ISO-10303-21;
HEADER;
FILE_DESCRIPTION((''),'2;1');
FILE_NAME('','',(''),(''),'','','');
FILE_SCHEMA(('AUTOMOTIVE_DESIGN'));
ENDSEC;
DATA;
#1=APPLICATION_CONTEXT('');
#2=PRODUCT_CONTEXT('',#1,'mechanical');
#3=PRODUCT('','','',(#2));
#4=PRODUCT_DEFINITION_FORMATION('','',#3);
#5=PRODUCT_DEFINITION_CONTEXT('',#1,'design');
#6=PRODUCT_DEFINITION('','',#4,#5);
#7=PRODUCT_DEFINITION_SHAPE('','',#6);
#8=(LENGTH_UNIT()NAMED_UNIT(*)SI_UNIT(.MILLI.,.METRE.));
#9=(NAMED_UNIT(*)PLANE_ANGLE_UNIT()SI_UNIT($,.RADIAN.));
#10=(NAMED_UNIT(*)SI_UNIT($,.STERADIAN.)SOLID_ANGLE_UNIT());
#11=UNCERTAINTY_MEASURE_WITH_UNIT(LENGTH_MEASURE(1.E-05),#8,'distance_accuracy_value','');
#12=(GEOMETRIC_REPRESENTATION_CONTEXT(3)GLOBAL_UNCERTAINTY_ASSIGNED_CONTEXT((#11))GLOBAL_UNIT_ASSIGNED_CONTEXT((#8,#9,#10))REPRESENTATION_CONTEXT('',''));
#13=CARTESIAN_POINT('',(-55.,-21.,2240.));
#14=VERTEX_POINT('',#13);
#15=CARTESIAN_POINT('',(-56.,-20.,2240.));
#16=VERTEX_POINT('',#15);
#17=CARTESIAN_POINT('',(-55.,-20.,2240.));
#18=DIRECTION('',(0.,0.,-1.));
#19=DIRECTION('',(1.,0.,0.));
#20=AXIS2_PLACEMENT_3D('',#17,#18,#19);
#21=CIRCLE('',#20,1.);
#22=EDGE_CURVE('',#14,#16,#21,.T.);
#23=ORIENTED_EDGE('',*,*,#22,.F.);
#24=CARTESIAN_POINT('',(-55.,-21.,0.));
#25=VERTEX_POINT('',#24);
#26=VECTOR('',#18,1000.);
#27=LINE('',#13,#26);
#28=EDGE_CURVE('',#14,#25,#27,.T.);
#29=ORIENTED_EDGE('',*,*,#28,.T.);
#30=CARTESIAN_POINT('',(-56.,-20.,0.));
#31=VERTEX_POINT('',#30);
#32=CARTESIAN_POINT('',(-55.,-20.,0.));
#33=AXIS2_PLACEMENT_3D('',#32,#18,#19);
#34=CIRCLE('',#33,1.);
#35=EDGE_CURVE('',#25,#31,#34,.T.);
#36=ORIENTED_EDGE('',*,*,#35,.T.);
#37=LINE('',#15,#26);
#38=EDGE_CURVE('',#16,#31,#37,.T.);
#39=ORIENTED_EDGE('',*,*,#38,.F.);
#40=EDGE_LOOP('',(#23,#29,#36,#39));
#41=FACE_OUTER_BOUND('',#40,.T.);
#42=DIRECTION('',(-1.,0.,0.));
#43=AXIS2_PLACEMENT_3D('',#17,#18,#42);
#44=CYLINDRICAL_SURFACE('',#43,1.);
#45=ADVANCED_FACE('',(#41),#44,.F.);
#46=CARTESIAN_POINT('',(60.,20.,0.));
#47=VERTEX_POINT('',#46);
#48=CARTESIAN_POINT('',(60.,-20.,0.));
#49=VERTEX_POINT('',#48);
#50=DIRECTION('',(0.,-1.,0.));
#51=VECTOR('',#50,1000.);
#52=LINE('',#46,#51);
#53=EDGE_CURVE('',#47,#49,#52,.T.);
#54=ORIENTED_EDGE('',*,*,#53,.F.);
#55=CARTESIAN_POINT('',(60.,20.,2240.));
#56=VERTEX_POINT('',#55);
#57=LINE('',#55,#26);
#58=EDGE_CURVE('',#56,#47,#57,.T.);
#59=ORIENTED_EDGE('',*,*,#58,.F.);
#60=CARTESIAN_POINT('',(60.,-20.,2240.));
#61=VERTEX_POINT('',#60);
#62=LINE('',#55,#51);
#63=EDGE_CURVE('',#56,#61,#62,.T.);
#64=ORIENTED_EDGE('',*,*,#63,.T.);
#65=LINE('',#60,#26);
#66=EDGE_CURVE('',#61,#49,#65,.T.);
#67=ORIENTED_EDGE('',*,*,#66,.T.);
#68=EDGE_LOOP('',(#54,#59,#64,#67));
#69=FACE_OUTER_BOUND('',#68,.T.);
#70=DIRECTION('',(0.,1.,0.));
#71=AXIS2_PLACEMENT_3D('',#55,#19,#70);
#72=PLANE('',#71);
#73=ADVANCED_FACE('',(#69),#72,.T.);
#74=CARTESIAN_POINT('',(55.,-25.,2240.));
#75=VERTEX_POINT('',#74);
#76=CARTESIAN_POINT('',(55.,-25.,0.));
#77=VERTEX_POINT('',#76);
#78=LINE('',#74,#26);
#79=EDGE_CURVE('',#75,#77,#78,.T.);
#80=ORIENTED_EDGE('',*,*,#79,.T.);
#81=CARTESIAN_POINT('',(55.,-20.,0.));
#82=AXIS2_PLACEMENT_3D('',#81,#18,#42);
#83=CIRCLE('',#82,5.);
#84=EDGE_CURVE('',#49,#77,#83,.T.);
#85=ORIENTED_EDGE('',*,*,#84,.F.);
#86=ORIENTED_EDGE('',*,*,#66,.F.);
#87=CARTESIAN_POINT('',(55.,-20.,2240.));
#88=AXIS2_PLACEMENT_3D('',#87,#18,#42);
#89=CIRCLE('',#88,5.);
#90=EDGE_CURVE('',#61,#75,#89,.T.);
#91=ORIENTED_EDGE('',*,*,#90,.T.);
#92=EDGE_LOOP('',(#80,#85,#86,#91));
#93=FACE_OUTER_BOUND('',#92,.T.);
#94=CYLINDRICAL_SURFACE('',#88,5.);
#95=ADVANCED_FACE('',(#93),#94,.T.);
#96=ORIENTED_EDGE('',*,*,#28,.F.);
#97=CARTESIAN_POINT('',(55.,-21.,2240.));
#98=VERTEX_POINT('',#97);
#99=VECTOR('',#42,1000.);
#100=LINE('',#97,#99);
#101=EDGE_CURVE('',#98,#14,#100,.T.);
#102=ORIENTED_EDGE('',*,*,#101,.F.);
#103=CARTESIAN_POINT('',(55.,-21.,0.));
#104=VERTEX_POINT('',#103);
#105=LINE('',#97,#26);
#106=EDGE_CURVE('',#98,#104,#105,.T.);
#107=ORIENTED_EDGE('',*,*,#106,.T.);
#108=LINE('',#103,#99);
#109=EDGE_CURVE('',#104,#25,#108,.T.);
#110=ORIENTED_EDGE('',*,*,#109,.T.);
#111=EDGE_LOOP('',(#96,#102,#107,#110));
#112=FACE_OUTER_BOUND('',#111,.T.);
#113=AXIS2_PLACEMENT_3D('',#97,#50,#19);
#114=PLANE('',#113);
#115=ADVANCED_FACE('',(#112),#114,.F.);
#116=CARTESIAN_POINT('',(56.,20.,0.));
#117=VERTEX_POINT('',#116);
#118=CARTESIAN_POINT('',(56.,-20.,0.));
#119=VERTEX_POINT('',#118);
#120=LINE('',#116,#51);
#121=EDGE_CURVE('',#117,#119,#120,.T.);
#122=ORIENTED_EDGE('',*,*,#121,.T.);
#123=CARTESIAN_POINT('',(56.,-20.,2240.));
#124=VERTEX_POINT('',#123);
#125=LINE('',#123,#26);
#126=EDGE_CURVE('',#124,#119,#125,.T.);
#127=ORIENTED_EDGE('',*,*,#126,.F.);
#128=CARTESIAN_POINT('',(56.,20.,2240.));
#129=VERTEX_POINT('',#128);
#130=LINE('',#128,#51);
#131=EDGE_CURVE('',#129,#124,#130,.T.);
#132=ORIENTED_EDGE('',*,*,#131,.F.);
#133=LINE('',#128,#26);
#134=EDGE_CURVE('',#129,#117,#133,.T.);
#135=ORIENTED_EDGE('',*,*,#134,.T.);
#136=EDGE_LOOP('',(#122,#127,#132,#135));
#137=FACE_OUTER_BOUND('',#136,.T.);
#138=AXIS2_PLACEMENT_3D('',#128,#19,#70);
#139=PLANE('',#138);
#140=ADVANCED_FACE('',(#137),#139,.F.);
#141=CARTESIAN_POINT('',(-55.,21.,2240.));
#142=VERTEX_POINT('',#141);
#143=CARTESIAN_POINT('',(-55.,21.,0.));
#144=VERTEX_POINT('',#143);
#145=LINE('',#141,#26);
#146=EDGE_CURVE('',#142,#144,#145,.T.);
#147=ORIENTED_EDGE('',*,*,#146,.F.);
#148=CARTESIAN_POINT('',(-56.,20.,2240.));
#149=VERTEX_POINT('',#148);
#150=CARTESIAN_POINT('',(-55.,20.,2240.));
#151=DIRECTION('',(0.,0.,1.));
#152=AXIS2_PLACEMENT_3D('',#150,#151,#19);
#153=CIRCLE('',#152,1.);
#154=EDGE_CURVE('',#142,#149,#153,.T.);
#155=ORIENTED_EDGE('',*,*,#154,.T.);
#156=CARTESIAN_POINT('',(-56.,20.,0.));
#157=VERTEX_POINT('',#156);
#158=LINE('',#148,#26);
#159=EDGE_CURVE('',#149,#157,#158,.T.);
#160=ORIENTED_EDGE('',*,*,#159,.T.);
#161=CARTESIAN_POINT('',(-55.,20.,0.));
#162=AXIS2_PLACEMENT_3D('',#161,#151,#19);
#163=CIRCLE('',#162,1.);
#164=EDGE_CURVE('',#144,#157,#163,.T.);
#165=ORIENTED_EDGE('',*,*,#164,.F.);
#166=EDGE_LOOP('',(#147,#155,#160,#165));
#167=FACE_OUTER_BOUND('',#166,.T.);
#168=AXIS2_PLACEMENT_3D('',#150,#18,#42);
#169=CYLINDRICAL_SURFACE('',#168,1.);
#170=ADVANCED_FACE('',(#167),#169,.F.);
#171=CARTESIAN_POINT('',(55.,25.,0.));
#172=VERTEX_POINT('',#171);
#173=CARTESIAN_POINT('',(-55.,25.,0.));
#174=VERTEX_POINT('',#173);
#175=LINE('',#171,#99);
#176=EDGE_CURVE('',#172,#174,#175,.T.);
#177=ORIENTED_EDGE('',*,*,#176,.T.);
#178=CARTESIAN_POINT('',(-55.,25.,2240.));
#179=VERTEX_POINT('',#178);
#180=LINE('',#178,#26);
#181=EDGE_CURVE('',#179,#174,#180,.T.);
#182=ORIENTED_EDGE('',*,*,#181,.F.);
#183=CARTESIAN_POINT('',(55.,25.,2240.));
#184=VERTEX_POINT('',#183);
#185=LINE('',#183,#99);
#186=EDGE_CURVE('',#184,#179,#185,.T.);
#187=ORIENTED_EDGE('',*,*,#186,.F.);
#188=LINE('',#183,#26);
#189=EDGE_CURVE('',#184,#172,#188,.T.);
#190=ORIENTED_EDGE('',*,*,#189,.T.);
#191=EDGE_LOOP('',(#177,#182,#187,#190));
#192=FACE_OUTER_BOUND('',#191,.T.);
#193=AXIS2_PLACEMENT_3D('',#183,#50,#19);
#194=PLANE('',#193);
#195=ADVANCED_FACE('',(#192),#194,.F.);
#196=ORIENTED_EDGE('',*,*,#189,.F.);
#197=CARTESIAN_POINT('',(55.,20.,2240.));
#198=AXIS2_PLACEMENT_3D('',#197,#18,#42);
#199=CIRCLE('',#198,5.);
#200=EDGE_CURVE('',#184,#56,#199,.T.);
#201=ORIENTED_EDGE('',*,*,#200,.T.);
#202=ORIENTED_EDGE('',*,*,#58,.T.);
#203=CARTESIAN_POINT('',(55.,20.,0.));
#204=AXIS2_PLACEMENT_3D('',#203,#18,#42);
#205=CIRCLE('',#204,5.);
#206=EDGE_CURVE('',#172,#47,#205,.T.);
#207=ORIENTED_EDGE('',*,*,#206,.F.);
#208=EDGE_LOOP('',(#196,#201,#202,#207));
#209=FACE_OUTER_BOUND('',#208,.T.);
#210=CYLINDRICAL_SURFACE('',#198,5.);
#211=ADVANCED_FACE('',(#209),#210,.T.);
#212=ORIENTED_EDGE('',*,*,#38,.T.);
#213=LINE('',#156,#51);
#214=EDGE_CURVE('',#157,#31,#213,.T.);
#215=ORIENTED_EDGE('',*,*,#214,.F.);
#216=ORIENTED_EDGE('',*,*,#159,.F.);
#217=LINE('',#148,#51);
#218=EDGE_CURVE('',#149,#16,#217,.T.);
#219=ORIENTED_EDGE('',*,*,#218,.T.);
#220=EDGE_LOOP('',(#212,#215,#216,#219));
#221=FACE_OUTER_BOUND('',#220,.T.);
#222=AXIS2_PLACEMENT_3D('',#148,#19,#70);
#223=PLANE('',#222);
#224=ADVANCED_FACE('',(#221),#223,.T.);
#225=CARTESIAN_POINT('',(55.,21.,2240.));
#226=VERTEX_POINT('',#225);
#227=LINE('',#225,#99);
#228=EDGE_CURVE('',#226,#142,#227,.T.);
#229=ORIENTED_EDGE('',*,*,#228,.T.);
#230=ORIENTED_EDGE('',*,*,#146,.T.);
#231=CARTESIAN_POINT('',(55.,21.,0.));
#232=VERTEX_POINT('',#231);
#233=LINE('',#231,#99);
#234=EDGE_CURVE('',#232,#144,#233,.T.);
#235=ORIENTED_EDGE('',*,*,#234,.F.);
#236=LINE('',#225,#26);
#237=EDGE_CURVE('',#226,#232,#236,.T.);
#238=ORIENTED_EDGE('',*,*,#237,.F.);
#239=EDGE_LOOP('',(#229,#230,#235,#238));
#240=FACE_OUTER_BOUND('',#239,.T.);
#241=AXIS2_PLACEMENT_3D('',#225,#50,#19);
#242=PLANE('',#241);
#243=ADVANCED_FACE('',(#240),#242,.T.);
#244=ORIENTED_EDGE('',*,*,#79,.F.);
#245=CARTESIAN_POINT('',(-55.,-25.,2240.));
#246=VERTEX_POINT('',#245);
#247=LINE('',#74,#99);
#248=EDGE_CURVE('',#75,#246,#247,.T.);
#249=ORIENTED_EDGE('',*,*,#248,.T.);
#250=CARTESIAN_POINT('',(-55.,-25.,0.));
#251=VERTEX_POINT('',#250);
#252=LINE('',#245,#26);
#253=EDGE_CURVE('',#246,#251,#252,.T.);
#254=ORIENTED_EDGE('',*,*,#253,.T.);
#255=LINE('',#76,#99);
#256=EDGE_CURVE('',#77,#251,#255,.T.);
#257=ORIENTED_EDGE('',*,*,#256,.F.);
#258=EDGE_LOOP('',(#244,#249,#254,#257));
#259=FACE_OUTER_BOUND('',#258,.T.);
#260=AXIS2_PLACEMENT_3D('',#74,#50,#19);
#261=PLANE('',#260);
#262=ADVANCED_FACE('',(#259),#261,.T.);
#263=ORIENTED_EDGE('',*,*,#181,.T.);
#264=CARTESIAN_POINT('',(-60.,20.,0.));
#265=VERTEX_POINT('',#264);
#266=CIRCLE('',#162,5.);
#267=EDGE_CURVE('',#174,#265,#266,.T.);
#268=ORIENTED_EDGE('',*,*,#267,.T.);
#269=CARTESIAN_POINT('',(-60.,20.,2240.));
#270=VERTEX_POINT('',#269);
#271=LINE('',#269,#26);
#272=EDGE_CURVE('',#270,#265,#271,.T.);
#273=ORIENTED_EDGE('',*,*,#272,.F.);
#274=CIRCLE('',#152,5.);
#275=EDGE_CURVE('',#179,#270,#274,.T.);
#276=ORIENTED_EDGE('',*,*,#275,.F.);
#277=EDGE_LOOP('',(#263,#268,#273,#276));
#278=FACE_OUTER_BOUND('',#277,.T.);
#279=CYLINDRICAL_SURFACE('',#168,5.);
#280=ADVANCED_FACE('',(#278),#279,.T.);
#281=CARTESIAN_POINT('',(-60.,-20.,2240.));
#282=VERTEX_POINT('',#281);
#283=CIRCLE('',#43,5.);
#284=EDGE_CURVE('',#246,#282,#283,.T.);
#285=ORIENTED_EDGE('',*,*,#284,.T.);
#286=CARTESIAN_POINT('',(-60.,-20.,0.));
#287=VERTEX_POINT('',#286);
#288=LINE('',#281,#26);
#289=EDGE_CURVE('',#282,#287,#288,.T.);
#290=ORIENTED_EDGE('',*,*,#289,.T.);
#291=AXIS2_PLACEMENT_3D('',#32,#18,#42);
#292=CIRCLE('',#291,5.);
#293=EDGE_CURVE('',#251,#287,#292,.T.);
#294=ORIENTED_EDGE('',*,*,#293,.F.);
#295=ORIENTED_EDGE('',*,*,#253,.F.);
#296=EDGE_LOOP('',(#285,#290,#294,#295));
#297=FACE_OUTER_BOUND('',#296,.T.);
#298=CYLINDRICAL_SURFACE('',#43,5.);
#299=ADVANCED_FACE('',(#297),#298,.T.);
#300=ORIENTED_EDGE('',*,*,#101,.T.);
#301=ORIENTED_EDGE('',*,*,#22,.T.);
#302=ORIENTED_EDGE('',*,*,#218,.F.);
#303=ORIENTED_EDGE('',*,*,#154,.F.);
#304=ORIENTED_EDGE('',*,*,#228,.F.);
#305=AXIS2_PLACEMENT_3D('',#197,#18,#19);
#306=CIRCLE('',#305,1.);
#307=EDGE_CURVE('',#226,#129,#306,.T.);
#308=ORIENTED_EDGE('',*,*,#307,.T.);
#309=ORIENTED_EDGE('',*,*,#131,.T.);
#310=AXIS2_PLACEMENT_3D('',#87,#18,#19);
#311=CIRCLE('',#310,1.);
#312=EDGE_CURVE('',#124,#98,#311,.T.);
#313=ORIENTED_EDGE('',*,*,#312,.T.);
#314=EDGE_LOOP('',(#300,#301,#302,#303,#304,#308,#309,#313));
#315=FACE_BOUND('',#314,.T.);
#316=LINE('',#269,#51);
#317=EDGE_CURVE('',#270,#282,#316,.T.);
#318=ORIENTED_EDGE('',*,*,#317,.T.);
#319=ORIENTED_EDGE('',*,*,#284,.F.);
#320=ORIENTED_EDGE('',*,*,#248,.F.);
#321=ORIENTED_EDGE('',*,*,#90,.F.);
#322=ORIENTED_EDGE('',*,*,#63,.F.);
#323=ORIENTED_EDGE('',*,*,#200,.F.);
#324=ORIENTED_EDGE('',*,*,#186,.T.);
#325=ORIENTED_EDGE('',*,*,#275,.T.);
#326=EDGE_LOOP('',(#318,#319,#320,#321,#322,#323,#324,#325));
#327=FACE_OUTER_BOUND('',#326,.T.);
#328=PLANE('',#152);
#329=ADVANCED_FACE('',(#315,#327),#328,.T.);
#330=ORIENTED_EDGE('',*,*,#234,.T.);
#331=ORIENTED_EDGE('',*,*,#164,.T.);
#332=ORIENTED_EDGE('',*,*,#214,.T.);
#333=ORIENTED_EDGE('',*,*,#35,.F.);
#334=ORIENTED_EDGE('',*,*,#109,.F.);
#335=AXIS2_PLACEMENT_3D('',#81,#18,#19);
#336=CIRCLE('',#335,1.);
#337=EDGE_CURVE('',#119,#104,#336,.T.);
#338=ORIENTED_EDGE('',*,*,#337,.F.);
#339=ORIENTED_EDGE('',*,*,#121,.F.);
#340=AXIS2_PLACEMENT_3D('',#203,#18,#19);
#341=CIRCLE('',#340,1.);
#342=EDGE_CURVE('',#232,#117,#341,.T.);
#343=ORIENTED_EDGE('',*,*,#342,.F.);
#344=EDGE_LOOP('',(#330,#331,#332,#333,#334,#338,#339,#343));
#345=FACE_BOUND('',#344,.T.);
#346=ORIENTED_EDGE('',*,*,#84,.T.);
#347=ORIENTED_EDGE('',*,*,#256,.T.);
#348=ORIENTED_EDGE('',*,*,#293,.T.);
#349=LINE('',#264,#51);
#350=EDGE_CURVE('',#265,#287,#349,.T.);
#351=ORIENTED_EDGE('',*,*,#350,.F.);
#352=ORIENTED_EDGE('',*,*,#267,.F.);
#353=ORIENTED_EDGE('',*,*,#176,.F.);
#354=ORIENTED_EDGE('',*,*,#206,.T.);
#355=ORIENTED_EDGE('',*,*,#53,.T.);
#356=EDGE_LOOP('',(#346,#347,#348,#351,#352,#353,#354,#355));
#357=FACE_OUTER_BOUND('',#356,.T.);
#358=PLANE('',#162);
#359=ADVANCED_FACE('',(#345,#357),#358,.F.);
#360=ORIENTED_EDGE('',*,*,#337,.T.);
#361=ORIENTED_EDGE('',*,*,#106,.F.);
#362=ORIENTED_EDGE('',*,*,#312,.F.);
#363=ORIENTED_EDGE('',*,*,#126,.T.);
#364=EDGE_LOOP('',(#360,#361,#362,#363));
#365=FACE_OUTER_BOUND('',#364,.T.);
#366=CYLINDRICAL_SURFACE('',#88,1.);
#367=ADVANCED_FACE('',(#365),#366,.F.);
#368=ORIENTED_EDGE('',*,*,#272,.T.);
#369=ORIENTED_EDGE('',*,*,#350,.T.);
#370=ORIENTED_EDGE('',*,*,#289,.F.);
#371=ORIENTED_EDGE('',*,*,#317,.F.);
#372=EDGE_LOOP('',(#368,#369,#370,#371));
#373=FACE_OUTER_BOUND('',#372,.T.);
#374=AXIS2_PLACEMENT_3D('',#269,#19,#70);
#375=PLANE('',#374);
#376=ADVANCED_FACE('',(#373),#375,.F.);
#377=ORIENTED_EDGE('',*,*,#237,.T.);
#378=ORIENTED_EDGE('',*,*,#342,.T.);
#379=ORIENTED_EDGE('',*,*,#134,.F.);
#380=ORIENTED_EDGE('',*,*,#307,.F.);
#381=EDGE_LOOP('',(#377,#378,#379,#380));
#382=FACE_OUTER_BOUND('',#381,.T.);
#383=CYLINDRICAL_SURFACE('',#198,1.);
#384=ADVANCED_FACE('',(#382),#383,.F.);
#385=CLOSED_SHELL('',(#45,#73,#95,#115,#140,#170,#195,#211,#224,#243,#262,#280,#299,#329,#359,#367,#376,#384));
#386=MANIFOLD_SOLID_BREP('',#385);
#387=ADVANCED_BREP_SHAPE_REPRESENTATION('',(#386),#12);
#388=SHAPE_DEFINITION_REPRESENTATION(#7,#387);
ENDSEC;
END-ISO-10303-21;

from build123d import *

# Parameters (mm, degrees)
BOSS_EXTRUDE1_DEPTH = 2240
SHELL1_T            = -4


with BuildPart() as part:
    # Sketch1 → Boss-Extrude1 (new body)
    with BuildSketch(Plane.XY):
        with BuildLine():
            Line((55, 25), (-55, 25))
            ThreePointArc((-55, 25), (-58.535533906, 23.535533906), (-60, 20))
            Line((-60, 20), (-60, -20))
            ThreePointArc((-60, -20), (-58.535533906, -23.535533906), (-55, -25))
            Line((-55, -25), (55, -25))
            ThreePointArc((55, -25), (58.535533906, -23.535533906), (60, -20))
            Line((60, -20), (60, 20))
            ThreePointArc((60, 20), (58.535533906, 23.535533906), (55, 25))
        make_face()
    extrude(amount=BOSS_EXTRUDE1_DEPTH)

    # Shell1
    shell1_openings = [part.faces().sort_by_distance(p)[0] for p in [
        (0, 0, 2240),
        (0, 0, 0),
    ]]
    offset(amount=SHELL1_T, openings=shell1_openings, kind=Kind.INTERSECTION)


solid = part.part
